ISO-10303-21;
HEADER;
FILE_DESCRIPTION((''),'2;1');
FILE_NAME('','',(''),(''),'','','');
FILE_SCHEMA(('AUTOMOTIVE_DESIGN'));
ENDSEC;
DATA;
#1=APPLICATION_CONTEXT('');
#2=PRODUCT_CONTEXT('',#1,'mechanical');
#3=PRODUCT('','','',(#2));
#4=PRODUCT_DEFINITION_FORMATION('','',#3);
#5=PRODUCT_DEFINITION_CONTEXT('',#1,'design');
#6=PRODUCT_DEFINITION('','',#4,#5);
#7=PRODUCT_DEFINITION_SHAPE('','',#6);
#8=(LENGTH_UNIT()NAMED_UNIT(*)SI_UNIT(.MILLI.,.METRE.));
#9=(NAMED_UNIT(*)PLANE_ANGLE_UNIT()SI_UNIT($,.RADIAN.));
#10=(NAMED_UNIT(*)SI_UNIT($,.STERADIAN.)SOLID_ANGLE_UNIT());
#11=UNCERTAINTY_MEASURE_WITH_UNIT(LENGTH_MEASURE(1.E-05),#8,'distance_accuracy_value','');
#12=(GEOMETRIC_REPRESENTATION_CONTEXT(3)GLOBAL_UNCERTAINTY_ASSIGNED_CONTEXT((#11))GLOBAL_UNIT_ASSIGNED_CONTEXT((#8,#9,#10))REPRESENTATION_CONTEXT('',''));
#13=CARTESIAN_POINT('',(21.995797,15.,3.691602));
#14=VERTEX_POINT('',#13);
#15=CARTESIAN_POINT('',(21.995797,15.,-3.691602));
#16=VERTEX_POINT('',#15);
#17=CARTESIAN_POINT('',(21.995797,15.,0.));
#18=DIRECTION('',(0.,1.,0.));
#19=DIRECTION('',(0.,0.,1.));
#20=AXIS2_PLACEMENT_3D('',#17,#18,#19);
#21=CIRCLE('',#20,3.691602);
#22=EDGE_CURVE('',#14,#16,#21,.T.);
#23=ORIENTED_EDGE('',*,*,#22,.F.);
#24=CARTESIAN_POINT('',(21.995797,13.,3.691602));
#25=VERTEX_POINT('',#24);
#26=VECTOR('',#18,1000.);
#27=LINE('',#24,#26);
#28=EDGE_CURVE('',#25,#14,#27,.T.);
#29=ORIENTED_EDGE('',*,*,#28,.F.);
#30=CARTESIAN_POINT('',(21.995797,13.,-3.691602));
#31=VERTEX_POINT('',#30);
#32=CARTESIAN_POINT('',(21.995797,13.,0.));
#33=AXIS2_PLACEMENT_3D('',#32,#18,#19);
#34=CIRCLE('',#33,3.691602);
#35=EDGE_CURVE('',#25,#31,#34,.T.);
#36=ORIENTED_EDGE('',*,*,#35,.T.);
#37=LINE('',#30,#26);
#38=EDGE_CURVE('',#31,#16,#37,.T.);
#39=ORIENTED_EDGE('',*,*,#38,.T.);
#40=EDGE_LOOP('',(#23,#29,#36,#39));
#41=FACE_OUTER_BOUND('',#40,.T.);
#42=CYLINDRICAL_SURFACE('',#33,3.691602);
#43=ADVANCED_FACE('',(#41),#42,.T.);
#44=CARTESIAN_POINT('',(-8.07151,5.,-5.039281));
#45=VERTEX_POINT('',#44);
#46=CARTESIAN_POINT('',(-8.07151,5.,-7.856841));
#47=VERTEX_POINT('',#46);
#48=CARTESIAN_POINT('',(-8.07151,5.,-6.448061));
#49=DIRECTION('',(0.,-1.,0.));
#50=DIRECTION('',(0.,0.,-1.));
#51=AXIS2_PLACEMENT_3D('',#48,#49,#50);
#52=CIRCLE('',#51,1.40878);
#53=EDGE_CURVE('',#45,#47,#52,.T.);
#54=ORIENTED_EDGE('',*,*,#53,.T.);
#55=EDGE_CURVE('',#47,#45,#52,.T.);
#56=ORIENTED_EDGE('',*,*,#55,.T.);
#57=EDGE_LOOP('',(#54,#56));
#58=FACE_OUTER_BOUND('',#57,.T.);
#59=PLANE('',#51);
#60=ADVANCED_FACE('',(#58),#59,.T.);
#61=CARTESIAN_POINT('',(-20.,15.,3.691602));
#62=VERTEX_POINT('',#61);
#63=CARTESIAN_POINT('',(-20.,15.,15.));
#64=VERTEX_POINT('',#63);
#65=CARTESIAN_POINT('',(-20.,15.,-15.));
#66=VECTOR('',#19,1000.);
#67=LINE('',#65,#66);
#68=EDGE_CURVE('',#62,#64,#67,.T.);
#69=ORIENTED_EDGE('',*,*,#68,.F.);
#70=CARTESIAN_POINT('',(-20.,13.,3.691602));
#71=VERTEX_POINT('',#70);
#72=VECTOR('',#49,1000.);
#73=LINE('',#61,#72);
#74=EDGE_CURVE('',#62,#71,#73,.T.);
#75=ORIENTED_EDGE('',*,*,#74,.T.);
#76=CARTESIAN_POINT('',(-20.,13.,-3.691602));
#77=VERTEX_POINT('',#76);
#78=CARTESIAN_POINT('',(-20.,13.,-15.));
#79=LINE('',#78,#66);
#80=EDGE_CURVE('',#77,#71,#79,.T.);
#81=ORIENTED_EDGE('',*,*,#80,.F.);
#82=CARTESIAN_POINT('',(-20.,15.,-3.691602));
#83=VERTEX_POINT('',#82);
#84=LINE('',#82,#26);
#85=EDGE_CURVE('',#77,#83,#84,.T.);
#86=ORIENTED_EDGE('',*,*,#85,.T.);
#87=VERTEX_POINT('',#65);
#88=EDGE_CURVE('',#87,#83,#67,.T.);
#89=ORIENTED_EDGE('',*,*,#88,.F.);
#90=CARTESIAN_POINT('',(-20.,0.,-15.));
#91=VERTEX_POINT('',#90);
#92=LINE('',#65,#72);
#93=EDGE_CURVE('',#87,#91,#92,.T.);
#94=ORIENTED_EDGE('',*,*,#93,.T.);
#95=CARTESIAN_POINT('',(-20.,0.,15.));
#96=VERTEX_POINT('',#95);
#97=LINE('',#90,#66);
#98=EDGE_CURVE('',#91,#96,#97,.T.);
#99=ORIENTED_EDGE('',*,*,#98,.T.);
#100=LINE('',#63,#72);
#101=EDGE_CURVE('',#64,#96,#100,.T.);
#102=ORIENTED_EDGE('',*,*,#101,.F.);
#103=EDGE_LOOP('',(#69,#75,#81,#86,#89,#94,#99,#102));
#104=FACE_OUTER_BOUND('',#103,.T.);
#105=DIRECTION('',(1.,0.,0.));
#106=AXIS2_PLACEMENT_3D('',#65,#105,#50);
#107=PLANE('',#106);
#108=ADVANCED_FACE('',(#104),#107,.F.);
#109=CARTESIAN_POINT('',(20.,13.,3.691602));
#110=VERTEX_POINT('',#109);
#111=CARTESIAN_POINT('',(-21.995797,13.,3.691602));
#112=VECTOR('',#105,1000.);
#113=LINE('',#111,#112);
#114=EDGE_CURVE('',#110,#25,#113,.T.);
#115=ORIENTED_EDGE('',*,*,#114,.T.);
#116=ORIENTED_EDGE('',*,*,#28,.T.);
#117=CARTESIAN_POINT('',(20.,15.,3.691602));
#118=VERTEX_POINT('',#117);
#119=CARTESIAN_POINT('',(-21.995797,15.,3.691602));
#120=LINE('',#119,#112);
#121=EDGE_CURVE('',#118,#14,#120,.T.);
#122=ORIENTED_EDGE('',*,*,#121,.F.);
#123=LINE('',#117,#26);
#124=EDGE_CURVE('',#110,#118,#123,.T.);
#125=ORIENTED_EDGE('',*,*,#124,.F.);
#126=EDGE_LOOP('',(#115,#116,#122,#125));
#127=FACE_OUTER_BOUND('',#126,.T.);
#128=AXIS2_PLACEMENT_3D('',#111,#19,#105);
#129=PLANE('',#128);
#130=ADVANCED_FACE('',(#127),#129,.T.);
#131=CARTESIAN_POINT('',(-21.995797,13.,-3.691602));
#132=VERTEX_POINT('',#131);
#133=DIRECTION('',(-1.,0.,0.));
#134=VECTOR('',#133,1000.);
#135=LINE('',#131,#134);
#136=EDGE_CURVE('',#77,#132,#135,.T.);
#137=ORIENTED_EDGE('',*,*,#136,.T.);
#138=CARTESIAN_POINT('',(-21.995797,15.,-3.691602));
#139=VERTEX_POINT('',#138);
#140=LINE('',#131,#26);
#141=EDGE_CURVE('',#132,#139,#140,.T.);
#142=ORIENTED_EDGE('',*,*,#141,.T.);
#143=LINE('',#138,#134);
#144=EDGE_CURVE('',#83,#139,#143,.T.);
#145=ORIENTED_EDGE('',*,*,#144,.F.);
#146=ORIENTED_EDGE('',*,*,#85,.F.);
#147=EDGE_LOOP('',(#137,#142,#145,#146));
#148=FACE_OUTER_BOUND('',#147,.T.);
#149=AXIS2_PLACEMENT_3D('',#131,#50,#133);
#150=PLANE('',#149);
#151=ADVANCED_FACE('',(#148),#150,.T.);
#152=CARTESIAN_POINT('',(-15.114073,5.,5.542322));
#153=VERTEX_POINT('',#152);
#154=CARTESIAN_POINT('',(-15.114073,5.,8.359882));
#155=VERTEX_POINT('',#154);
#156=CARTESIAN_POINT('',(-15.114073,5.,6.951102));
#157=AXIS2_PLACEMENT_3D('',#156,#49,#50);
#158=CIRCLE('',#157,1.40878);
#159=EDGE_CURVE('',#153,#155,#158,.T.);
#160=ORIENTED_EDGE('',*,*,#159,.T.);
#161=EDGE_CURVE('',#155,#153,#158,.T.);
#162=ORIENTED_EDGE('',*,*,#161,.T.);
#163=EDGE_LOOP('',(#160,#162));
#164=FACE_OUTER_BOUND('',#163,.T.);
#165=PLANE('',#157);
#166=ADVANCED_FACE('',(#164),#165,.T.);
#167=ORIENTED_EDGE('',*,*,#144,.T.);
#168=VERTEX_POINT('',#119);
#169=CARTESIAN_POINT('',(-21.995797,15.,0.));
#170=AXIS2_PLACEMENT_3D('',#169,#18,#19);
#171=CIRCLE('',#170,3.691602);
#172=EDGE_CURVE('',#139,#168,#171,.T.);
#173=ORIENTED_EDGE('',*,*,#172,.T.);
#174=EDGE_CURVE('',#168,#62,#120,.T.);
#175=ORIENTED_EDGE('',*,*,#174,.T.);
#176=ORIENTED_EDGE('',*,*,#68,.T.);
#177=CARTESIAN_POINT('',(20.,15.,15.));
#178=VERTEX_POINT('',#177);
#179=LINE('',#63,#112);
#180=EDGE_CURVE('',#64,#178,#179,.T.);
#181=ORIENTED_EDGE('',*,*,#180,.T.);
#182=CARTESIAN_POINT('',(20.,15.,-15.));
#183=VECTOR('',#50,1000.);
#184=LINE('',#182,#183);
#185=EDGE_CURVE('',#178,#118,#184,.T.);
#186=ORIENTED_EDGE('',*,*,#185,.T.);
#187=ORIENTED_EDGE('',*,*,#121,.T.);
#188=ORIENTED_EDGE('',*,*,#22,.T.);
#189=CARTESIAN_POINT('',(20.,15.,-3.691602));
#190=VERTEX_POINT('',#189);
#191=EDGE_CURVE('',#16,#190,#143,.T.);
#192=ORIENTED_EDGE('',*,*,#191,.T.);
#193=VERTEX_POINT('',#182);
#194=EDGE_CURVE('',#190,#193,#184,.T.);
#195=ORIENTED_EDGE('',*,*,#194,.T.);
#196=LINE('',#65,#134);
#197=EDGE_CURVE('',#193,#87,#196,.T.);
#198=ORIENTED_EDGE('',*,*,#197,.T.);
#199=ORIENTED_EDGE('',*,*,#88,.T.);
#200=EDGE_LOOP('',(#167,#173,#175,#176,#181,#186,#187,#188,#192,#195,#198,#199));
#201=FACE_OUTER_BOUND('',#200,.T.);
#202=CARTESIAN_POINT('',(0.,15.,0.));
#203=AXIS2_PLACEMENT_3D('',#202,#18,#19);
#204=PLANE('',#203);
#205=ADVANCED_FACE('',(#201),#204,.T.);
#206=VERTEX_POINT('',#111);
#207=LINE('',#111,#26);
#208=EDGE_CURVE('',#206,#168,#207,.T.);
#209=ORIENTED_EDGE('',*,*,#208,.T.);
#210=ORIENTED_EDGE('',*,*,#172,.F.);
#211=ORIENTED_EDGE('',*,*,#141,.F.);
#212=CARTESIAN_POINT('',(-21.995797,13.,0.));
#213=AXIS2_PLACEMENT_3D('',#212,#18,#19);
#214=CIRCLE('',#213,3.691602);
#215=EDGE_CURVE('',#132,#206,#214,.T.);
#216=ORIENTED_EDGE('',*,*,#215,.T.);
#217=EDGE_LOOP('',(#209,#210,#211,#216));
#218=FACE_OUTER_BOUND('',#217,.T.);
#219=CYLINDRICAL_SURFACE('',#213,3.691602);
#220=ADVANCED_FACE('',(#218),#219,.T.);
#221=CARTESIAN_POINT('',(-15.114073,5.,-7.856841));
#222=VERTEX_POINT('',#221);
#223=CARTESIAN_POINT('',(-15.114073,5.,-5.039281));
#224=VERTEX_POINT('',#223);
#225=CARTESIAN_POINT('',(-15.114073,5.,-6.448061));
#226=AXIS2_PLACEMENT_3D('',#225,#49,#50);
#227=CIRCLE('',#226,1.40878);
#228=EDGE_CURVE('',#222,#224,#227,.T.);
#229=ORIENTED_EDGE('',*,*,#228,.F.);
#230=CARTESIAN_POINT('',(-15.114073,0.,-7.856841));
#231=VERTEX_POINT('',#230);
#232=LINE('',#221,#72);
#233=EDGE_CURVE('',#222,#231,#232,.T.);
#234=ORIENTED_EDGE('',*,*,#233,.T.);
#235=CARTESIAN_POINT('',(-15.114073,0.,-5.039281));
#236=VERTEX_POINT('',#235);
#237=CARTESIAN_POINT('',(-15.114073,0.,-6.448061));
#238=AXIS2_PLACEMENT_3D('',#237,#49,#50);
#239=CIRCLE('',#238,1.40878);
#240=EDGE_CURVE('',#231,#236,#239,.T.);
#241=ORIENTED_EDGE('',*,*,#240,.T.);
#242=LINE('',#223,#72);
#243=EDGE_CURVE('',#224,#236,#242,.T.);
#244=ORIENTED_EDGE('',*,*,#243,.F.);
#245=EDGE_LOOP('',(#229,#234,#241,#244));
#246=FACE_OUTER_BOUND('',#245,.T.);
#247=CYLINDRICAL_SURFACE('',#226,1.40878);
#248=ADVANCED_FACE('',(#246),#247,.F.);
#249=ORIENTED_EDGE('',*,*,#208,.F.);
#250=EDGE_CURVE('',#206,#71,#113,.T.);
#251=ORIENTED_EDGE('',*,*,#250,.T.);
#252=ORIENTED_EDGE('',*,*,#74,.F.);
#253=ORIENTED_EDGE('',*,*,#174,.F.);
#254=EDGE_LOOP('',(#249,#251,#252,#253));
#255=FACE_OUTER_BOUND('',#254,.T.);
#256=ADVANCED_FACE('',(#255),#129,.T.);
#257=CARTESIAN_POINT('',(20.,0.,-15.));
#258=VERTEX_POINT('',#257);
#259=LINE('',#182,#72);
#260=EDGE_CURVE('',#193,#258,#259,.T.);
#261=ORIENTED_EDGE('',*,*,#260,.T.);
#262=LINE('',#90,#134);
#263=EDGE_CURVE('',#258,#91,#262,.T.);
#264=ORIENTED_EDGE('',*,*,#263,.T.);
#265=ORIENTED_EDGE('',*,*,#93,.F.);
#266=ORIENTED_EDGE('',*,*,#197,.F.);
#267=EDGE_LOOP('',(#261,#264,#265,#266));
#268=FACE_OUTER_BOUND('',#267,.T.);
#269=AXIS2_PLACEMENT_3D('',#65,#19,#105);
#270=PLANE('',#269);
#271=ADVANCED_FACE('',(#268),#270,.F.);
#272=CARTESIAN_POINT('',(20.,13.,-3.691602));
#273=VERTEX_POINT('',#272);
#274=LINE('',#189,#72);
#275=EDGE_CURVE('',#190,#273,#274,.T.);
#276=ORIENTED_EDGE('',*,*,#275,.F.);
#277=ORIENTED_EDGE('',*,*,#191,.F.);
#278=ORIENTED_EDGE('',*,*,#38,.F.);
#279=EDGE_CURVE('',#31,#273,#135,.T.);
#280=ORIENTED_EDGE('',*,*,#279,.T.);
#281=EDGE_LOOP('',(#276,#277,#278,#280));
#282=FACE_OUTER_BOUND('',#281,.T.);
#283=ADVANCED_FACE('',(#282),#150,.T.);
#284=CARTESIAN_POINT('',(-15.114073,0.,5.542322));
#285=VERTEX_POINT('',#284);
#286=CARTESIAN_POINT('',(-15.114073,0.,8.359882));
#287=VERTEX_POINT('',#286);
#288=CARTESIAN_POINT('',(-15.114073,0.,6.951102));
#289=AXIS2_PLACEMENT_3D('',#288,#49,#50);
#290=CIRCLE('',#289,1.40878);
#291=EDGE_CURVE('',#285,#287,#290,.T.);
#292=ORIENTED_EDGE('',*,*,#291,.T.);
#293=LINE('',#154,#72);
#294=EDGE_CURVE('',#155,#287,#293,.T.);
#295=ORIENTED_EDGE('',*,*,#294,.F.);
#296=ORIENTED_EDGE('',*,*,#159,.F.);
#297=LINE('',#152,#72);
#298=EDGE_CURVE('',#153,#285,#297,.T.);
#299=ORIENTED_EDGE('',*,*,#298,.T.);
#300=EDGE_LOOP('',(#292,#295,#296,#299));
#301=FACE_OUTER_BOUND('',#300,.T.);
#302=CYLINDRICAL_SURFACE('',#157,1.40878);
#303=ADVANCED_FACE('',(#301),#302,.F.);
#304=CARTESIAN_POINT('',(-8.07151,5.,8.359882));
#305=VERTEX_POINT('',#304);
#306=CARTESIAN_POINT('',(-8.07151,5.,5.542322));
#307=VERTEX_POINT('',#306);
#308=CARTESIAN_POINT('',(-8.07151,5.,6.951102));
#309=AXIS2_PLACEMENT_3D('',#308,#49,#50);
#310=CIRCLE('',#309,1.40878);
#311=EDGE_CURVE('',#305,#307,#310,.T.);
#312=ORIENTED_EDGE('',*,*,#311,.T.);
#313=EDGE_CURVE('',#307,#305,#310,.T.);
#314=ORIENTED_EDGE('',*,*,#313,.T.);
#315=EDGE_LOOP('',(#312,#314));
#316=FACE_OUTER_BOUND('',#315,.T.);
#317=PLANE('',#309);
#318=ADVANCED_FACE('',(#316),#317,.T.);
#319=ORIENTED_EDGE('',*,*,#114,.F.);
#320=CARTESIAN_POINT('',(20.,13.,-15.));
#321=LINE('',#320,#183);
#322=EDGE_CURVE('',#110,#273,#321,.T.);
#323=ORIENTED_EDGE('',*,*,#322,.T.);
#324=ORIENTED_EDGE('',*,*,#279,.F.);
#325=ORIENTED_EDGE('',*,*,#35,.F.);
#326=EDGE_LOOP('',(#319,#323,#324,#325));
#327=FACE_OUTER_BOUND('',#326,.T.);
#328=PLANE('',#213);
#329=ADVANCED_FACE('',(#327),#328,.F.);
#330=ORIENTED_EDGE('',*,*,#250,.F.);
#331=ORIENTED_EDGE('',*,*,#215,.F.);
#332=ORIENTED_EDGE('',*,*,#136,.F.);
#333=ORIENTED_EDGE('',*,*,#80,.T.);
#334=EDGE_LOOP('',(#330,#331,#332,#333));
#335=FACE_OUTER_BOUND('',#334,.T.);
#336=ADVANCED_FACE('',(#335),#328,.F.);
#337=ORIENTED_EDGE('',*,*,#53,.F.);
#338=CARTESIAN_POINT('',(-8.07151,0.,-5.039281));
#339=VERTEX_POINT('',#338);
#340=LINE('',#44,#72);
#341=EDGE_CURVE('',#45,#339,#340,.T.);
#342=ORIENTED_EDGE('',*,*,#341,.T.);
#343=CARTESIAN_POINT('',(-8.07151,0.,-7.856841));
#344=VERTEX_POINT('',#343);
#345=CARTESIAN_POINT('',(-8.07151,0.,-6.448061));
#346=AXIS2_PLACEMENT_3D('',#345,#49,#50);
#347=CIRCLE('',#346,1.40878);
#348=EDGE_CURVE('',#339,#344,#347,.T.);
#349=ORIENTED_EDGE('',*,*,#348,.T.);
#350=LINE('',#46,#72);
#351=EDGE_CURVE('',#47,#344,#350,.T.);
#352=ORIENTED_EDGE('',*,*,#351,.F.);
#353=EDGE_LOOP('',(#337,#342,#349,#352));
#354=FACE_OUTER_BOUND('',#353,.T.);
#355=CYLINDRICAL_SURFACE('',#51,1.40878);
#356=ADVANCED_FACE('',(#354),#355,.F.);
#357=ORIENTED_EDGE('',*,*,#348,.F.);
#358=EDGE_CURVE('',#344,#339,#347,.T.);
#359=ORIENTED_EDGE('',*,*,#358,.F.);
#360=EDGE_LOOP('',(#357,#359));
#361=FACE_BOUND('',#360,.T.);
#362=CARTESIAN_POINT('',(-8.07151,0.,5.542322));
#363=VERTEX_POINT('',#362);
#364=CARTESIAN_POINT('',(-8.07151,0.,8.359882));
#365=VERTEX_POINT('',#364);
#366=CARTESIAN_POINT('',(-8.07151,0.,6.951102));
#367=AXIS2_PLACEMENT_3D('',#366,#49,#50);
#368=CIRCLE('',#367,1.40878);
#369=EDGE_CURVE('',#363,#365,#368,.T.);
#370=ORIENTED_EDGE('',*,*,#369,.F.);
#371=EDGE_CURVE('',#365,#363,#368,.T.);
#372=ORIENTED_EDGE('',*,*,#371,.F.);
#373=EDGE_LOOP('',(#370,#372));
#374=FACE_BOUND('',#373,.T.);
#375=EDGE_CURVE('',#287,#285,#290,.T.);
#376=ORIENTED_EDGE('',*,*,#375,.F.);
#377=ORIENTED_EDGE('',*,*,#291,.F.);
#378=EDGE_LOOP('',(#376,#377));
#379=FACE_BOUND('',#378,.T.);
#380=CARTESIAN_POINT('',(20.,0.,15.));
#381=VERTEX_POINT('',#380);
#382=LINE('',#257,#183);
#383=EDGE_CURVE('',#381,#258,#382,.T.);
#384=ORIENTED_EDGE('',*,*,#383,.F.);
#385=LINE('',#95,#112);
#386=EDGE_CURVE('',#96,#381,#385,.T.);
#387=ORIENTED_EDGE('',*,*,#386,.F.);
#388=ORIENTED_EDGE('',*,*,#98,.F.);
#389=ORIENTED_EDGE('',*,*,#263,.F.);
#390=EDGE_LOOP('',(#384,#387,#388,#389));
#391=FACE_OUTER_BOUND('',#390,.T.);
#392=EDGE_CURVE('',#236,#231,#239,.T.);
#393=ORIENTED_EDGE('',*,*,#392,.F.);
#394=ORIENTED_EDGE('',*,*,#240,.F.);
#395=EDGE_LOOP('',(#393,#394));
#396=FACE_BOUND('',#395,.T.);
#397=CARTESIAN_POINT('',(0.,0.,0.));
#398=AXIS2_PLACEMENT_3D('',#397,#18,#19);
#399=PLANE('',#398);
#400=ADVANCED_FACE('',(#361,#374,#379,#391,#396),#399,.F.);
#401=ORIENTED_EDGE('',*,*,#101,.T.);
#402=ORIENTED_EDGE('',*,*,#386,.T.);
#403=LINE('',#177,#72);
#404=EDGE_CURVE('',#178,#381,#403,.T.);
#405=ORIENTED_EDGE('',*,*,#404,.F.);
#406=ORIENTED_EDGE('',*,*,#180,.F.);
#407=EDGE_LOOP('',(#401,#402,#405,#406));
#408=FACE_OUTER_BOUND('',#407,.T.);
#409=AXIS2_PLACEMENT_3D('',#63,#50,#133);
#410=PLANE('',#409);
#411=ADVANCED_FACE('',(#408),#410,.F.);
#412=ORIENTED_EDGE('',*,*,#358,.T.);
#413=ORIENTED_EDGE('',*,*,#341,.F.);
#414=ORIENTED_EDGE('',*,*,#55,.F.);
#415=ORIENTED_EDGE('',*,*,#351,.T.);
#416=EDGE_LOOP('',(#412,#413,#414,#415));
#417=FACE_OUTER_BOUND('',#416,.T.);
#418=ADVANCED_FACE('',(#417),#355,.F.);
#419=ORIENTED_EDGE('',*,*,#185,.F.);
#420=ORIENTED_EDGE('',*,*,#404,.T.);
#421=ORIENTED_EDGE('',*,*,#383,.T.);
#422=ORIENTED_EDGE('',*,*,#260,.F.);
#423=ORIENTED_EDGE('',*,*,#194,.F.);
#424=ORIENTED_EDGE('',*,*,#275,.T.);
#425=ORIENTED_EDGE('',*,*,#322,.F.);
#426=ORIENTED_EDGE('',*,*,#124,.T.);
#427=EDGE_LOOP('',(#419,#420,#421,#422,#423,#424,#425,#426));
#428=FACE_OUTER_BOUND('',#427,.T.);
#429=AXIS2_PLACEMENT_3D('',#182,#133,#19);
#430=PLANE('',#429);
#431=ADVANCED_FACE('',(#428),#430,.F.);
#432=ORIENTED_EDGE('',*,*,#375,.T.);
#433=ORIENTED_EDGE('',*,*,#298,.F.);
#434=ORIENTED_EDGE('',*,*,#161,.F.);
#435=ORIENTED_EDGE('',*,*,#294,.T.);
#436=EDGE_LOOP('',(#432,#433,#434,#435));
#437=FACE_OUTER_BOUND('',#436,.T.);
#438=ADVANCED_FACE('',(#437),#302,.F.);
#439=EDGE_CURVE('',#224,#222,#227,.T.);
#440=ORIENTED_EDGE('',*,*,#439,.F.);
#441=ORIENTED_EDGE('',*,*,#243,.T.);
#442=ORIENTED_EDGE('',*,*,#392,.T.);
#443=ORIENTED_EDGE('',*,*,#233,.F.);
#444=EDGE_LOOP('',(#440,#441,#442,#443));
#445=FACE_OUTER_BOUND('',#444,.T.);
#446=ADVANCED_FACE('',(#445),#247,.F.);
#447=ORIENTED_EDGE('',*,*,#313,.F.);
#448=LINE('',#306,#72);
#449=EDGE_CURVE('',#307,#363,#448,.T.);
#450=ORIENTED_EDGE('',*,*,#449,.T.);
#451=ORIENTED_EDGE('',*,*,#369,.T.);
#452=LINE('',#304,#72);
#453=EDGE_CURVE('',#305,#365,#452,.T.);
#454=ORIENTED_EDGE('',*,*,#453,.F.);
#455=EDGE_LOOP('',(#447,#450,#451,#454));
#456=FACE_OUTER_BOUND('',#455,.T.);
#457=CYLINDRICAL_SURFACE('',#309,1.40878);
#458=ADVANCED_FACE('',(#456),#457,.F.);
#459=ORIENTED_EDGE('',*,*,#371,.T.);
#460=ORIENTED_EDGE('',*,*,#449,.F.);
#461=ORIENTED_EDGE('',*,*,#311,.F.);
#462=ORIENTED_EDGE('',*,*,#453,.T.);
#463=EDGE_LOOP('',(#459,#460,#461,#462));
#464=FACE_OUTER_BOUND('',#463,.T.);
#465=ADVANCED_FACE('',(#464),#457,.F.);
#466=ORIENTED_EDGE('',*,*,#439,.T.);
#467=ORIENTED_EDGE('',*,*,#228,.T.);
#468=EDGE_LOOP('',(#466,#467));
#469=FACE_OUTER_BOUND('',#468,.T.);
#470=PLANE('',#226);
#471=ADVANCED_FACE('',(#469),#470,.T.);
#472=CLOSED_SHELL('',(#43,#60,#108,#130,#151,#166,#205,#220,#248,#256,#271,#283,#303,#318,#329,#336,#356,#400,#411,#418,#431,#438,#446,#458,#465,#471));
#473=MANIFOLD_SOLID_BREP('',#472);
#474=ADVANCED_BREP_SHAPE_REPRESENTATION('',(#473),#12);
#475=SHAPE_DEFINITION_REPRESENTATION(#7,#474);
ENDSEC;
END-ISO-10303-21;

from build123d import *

# Parameters (mm, degrees)
SKETCH1_W           = 40
SKETCH1_H           = 30
BOSS_EXTRUDE1_DEPTH = 15
BOSS_EXTRUDE2_DEPTH = 2
SKETCH3_R           = 1.408779943
CUT_EXTRUDE1_DEPTH  = 5


with BuildPart() as part:
    # Sketch1 → Boss-Extrude1 (new body)
    with BuildSketch(Plane(origin=(0, 0, 0), x_dir=(1, 0, 0), z_dir=(0, 1, 0))):
        Rectangle(SKETCH1_W, SKETCH1_H)
    extrude(amount=BOSS_EXTRUDE1_DEPTH)

    # Sketch2 → Boss-Extrude2 (add)
    with BuildSketch(Plane(origin=(0, 15, 0), x_dir=(1, 0, 0), z_dir=(0, 1, 0))):
        with BuildLine():
            Line((-21.995796848, 3.691602268), (21.995796848, 3.691602268))
            ThreePointArc((21.995796848, 3.691602268), (25.687399116, 0), (21.995796848, -3.691602268))
            Line((21.995796848, -3.691602268), (-21.995796848, -3.691602268))
            ThreePointArc((-21.995796848, -3.691602268), (-25.687399116, 0), (-21.995796848, 3.691602268))
        make_face()
    extrude(amount=-BOSS_EXTRUDE2_DEPTH)

    # Sketch3 → Cut-Extrude1 (cut)
    with BuildSketch(Plane.XZ):
        with Locations(Location((-15.114073065, 6.951101682, 0), (0, 0, 270))):
            Circle(SKETCH3_R)
        with Locations(Location((-8.071509519, 6.951101682, 0), (0, 0, 270))):
            Circle(SKETCH3_R)
        with Locations(Location((-15.114073065, -6.448061429, 0), (0, 0, 270))):
            Circle(SKETCH3_R)
        with Locations(Location((-8.071509519, -6.448061429, 0), (0, 0, 270))):
            Circle(SKETCH3_R)
    extrude(amount=-CUT_EXTRUDE1_DEPTH, mode=Mode.SUBTRACT)


solid = part.part
